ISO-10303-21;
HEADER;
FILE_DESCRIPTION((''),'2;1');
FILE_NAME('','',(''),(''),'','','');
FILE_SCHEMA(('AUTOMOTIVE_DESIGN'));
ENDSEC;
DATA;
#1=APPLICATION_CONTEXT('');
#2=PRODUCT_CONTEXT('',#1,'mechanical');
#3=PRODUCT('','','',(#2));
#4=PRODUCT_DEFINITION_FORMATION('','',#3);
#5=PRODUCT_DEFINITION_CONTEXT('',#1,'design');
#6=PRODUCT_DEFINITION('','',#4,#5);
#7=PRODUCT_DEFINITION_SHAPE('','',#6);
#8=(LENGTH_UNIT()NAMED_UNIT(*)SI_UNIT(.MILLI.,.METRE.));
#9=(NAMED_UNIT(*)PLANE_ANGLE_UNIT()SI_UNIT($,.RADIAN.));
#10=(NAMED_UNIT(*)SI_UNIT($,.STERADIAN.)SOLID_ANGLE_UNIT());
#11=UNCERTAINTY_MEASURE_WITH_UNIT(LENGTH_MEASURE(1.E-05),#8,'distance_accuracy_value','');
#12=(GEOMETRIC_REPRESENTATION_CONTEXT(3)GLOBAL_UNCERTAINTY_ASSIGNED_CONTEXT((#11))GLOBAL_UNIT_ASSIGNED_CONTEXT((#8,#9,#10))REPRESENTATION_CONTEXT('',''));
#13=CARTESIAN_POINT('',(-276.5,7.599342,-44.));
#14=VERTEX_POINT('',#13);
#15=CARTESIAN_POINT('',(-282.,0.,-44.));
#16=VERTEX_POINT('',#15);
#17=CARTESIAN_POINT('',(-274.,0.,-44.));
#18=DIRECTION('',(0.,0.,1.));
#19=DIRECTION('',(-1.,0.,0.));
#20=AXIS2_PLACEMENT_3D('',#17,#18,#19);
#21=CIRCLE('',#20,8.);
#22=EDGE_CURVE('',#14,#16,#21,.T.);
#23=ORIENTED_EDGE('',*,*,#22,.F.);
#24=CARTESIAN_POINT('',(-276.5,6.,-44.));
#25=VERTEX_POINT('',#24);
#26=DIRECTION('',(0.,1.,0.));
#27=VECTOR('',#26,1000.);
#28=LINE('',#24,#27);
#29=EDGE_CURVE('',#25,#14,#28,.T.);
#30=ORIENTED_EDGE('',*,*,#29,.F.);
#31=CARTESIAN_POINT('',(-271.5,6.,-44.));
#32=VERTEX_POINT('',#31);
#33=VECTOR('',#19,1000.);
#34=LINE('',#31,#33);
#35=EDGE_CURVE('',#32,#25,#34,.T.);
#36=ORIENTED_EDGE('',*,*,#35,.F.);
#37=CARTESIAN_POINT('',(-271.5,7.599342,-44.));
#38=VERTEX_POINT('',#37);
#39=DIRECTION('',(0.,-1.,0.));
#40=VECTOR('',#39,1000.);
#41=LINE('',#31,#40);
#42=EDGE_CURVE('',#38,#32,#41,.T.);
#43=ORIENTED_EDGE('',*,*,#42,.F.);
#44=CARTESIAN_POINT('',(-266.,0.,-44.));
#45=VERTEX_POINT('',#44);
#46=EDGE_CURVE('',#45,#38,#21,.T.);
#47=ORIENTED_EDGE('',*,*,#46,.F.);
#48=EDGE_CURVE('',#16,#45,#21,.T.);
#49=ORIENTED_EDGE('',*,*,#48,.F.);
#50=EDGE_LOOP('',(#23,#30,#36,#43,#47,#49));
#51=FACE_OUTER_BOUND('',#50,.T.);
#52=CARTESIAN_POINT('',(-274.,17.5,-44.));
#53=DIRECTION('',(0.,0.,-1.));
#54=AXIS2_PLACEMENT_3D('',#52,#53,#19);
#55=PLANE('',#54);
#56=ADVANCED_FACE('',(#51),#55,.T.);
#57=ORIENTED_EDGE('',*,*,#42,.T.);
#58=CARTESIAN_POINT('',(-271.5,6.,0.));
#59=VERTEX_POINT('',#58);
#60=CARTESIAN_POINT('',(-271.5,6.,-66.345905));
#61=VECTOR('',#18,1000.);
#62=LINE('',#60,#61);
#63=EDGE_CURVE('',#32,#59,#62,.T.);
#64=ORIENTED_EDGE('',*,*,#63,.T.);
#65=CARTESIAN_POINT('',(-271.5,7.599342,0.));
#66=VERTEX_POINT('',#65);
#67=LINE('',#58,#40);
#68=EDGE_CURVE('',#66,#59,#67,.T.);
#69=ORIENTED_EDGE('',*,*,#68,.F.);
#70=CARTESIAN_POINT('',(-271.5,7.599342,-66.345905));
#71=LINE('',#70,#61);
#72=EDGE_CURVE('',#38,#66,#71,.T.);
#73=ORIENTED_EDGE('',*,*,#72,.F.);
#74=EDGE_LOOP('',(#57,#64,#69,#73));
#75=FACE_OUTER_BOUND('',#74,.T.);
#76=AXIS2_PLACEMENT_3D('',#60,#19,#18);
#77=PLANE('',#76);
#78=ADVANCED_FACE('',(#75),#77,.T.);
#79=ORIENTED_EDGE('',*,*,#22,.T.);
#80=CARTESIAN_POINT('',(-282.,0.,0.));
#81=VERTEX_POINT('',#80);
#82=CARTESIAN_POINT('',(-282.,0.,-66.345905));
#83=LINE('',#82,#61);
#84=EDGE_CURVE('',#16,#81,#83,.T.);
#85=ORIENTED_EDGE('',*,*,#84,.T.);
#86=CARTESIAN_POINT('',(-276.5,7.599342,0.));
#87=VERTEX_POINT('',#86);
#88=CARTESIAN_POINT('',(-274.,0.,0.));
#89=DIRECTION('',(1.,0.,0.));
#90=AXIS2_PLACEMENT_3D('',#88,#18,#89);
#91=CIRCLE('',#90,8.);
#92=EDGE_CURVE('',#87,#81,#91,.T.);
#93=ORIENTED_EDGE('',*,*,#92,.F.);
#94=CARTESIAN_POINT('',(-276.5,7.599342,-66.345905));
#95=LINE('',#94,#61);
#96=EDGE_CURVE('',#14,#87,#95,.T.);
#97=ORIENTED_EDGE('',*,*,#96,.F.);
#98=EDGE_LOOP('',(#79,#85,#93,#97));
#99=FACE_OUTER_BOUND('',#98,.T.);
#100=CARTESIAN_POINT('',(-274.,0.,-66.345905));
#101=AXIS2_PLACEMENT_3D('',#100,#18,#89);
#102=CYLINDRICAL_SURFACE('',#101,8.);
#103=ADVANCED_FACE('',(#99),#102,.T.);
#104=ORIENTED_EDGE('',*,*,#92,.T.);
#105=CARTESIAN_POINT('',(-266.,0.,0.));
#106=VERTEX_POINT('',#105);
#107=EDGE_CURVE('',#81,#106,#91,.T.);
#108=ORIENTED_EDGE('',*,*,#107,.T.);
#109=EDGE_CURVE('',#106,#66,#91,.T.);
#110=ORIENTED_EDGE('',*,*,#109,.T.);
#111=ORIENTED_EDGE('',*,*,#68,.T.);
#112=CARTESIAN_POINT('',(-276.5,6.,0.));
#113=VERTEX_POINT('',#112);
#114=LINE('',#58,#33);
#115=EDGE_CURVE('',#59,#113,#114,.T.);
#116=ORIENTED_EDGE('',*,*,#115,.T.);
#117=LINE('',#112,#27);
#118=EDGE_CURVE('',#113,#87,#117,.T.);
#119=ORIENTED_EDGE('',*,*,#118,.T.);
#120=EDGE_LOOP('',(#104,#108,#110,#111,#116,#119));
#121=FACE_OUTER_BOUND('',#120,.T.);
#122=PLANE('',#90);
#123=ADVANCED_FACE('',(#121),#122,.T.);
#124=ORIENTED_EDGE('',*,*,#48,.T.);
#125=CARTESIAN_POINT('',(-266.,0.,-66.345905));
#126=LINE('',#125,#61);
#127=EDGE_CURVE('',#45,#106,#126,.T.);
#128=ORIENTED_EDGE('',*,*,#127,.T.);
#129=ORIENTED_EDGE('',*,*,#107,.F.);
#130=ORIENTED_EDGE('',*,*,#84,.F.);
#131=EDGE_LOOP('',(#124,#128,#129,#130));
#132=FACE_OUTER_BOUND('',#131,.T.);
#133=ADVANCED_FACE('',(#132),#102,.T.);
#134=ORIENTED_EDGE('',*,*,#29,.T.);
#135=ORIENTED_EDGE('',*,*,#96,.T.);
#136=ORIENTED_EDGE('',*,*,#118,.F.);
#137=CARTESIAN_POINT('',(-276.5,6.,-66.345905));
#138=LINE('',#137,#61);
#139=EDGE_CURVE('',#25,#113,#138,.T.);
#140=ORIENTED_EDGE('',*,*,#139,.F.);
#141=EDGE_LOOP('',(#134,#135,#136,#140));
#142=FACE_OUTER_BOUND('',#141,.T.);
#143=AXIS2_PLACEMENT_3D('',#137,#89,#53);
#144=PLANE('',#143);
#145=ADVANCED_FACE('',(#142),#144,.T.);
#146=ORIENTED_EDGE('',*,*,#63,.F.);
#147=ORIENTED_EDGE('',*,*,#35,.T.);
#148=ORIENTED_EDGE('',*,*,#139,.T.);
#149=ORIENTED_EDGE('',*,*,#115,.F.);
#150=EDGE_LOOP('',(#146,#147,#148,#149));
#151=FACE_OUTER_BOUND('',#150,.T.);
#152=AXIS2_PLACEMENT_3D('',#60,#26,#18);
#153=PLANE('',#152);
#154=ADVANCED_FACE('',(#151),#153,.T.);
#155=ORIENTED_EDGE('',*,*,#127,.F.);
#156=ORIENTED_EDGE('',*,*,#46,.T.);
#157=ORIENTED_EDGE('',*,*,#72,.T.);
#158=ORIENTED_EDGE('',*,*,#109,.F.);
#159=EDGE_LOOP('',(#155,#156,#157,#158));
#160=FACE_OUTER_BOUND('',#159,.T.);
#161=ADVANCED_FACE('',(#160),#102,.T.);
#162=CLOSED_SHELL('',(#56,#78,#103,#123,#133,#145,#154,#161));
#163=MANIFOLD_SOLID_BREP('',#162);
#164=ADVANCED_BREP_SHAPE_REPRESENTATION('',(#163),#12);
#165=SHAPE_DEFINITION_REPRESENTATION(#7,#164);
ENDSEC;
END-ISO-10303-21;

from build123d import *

# Parameters (mm, degrees)
BOSS_EXTRUDE1_DEPTH = 44


with BuildPart() as part:
    # Sketch1 → Boss-Extrude1 (new body)
    with BuildSketch(Plane.XY):
        with BuildLine():
            Line((-271.5, 6), (-271.5, 7.599342077))
            ThreePointArc((-271.5, 7.599342077), (-274, -8), (-276.5, 7.599342077))
            Line((-276.5, 7.599342077), (-276.5, 6))
            Line((-276.5, 6), (-271.5, 6))
        make_face()
    extrude(amount=-BOSS_EXTRUDE1_DEPTH)


solid = part.part
